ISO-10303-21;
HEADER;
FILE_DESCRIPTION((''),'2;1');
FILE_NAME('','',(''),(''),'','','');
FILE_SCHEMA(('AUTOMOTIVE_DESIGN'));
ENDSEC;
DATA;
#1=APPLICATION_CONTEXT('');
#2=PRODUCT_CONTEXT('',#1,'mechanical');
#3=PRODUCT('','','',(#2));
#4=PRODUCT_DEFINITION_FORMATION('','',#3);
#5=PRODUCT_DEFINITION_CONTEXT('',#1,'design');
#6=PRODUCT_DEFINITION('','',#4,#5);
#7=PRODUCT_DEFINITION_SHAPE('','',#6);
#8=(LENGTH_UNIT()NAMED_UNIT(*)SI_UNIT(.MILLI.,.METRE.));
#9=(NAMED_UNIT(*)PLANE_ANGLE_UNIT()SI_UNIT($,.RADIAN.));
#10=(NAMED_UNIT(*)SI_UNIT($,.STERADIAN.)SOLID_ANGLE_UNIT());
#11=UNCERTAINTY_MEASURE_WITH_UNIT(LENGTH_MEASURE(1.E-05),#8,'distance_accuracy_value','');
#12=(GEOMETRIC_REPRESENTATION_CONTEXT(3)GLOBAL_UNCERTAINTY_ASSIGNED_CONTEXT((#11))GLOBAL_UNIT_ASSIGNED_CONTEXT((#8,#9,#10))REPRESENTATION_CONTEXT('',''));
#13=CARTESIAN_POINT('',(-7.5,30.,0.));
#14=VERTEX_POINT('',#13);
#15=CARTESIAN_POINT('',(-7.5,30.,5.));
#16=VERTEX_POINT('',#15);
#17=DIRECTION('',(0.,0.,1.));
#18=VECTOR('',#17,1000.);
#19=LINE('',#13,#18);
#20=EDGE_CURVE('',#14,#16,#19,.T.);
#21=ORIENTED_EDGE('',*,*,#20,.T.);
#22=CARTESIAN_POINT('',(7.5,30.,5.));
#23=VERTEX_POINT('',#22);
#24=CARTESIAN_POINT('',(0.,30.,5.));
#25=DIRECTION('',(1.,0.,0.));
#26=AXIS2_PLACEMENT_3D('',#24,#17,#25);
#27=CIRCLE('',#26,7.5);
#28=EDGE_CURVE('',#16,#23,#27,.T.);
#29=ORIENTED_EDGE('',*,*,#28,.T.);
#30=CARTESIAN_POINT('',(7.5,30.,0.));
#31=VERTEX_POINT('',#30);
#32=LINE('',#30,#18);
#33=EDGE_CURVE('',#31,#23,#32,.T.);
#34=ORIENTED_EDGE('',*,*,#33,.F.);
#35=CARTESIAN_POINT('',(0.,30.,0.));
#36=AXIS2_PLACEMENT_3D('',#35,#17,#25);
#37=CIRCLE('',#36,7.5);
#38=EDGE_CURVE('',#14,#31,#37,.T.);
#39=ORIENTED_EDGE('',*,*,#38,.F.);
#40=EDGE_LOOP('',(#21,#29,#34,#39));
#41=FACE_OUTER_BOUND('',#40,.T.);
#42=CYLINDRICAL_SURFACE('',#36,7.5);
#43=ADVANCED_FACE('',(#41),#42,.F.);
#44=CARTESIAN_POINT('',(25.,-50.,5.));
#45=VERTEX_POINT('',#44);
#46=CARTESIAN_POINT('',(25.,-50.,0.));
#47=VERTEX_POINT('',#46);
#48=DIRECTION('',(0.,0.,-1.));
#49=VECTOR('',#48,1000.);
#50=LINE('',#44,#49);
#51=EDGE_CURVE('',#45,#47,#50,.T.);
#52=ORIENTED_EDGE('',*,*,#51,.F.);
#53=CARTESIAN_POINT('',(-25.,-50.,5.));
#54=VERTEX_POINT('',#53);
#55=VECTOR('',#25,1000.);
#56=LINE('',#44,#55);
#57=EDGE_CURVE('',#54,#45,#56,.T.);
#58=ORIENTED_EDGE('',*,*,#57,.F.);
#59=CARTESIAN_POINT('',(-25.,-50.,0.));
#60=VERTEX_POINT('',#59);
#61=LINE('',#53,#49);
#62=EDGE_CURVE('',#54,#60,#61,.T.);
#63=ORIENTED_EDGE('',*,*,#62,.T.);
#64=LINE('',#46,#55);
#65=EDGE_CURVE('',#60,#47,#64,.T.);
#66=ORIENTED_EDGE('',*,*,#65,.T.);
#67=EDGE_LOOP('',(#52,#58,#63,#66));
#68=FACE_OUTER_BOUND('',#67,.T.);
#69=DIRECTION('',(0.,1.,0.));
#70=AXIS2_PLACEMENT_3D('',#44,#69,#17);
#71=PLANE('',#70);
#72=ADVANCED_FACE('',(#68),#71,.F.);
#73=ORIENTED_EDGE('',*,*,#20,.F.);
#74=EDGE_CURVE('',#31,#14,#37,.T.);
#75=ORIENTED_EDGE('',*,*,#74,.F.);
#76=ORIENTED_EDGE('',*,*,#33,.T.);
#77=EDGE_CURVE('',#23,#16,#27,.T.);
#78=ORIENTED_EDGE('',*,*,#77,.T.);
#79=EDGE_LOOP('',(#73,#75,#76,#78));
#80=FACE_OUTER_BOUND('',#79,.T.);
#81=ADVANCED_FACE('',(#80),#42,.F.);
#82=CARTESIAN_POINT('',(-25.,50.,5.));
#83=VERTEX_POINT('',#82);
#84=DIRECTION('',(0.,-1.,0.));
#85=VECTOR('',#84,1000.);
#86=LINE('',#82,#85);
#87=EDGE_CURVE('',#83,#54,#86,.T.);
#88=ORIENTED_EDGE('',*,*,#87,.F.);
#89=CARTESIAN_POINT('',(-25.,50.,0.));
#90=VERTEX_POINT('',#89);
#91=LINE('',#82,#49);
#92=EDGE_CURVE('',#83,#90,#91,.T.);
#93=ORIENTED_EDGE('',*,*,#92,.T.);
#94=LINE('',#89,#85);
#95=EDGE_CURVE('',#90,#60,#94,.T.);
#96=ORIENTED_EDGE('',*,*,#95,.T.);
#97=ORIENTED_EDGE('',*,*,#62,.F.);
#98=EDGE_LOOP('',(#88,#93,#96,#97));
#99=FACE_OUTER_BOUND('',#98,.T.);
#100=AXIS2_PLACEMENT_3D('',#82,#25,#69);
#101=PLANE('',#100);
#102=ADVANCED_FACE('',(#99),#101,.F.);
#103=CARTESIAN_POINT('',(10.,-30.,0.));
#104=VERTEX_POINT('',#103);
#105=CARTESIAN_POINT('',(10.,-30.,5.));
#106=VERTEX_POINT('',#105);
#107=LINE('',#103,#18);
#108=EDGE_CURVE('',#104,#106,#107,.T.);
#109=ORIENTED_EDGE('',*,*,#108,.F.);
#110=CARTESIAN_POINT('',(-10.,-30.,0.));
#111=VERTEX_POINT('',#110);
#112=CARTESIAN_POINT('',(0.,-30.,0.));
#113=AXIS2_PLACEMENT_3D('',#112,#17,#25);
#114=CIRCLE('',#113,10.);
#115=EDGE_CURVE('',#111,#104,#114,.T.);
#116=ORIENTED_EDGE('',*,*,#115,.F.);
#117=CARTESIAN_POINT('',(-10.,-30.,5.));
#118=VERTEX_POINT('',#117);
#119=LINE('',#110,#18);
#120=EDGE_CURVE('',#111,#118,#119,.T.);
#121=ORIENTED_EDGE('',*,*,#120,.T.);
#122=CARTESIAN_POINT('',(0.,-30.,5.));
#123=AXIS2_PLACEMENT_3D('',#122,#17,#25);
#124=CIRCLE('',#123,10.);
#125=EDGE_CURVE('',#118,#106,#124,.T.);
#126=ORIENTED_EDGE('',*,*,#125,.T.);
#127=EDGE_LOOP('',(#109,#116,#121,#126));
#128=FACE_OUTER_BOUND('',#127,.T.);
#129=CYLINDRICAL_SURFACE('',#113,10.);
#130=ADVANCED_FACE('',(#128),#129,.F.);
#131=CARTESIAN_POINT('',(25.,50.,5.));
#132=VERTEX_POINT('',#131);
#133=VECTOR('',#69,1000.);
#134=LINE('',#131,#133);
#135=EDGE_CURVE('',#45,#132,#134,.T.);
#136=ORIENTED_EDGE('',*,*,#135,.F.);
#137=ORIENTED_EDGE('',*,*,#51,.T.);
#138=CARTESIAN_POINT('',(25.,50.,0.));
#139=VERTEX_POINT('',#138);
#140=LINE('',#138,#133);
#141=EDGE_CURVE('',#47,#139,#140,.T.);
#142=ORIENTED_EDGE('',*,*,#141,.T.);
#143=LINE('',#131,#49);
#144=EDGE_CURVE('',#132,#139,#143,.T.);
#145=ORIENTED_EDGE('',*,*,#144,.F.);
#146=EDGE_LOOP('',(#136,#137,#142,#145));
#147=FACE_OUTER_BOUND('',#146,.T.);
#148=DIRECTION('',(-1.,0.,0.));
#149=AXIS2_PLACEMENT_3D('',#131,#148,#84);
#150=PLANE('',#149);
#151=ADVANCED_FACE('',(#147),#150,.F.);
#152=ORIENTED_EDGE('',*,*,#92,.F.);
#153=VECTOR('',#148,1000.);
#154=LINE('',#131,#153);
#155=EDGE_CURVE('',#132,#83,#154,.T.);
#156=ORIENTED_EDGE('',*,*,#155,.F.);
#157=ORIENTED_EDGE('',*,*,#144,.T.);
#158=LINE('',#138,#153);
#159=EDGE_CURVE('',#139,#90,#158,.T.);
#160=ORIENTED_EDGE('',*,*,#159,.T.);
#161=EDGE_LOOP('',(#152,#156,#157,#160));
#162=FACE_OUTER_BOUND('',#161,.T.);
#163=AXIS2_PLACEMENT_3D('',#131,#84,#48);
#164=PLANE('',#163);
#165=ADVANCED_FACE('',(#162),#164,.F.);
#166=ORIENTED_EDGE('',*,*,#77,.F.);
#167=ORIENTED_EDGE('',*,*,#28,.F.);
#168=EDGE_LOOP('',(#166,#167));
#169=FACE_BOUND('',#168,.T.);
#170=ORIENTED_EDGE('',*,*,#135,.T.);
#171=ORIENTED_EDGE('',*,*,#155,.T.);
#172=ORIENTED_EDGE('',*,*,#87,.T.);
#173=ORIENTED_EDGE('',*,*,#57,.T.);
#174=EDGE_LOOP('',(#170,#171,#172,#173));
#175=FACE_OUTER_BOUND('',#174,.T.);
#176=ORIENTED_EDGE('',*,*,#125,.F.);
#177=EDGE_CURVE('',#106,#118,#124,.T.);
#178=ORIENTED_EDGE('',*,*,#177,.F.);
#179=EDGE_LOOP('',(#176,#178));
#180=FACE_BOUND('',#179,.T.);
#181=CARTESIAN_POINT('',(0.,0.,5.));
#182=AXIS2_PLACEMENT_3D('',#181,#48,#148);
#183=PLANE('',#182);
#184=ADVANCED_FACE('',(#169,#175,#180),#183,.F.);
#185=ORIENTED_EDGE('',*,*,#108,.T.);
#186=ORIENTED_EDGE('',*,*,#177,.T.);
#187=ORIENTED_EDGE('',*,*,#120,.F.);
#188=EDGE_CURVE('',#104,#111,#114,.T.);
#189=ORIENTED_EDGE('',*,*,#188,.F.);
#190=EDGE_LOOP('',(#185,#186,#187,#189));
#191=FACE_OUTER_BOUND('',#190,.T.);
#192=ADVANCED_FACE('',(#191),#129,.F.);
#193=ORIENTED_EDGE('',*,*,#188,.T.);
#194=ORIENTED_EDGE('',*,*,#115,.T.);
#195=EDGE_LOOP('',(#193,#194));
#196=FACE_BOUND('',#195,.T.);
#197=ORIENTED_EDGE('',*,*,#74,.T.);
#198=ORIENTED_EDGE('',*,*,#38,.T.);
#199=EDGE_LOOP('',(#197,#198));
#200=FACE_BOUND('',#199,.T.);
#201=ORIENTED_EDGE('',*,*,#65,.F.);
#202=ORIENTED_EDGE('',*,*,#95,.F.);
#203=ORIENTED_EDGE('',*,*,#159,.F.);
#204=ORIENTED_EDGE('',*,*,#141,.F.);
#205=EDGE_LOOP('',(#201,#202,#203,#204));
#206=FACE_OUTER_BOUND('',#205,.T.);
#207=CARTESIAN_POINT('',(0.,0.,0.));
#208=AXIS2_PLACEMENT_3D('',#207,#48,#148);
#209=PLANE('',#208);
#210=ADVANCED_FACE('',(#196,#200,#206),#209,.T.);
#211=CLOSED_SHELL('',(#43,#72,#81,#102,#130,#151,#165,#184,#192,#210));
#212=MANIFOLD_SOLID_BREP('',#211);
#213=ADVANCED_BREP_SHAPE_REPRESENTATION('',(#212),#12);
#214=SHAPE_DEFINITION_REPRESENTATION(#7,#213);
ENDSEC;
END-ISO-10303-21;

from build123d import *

# Parameters (mm, degrees)
SKETCH1_W           = 50
SKETCH1_H           = 100
BOSS_EXTRUDE1_DEPTH = 5
SKETCH2_R           = 10
SKETCH2_R_2         = 7.5
CUT_EXTRUDE1_DEPTH  = 5


with BuildPart() as part:
    # Sketch1 → Boss-Extrude1 (new body)
    with BuildSketch(Plane.XY):
        Rectangle(SKETCH1_W, SKETCH1_H)
    extrude(amount=BOSS_EXTRUDE1_DEPTH)

    # Sketch2 → Cut-Extrude1 (cut)
    with BuildSketch(Plane.XY.offset(5)):
        with Locations((0, -30)):
            Circle(SKETCH2_R)
        with Locations((0, 30)):
            Circle(SKETCH2_R_2)
    extrude(amount=-CUT_EXTRUDE1_DEPTH, mode=Mode.SUBTRACT)


solid = part.part
